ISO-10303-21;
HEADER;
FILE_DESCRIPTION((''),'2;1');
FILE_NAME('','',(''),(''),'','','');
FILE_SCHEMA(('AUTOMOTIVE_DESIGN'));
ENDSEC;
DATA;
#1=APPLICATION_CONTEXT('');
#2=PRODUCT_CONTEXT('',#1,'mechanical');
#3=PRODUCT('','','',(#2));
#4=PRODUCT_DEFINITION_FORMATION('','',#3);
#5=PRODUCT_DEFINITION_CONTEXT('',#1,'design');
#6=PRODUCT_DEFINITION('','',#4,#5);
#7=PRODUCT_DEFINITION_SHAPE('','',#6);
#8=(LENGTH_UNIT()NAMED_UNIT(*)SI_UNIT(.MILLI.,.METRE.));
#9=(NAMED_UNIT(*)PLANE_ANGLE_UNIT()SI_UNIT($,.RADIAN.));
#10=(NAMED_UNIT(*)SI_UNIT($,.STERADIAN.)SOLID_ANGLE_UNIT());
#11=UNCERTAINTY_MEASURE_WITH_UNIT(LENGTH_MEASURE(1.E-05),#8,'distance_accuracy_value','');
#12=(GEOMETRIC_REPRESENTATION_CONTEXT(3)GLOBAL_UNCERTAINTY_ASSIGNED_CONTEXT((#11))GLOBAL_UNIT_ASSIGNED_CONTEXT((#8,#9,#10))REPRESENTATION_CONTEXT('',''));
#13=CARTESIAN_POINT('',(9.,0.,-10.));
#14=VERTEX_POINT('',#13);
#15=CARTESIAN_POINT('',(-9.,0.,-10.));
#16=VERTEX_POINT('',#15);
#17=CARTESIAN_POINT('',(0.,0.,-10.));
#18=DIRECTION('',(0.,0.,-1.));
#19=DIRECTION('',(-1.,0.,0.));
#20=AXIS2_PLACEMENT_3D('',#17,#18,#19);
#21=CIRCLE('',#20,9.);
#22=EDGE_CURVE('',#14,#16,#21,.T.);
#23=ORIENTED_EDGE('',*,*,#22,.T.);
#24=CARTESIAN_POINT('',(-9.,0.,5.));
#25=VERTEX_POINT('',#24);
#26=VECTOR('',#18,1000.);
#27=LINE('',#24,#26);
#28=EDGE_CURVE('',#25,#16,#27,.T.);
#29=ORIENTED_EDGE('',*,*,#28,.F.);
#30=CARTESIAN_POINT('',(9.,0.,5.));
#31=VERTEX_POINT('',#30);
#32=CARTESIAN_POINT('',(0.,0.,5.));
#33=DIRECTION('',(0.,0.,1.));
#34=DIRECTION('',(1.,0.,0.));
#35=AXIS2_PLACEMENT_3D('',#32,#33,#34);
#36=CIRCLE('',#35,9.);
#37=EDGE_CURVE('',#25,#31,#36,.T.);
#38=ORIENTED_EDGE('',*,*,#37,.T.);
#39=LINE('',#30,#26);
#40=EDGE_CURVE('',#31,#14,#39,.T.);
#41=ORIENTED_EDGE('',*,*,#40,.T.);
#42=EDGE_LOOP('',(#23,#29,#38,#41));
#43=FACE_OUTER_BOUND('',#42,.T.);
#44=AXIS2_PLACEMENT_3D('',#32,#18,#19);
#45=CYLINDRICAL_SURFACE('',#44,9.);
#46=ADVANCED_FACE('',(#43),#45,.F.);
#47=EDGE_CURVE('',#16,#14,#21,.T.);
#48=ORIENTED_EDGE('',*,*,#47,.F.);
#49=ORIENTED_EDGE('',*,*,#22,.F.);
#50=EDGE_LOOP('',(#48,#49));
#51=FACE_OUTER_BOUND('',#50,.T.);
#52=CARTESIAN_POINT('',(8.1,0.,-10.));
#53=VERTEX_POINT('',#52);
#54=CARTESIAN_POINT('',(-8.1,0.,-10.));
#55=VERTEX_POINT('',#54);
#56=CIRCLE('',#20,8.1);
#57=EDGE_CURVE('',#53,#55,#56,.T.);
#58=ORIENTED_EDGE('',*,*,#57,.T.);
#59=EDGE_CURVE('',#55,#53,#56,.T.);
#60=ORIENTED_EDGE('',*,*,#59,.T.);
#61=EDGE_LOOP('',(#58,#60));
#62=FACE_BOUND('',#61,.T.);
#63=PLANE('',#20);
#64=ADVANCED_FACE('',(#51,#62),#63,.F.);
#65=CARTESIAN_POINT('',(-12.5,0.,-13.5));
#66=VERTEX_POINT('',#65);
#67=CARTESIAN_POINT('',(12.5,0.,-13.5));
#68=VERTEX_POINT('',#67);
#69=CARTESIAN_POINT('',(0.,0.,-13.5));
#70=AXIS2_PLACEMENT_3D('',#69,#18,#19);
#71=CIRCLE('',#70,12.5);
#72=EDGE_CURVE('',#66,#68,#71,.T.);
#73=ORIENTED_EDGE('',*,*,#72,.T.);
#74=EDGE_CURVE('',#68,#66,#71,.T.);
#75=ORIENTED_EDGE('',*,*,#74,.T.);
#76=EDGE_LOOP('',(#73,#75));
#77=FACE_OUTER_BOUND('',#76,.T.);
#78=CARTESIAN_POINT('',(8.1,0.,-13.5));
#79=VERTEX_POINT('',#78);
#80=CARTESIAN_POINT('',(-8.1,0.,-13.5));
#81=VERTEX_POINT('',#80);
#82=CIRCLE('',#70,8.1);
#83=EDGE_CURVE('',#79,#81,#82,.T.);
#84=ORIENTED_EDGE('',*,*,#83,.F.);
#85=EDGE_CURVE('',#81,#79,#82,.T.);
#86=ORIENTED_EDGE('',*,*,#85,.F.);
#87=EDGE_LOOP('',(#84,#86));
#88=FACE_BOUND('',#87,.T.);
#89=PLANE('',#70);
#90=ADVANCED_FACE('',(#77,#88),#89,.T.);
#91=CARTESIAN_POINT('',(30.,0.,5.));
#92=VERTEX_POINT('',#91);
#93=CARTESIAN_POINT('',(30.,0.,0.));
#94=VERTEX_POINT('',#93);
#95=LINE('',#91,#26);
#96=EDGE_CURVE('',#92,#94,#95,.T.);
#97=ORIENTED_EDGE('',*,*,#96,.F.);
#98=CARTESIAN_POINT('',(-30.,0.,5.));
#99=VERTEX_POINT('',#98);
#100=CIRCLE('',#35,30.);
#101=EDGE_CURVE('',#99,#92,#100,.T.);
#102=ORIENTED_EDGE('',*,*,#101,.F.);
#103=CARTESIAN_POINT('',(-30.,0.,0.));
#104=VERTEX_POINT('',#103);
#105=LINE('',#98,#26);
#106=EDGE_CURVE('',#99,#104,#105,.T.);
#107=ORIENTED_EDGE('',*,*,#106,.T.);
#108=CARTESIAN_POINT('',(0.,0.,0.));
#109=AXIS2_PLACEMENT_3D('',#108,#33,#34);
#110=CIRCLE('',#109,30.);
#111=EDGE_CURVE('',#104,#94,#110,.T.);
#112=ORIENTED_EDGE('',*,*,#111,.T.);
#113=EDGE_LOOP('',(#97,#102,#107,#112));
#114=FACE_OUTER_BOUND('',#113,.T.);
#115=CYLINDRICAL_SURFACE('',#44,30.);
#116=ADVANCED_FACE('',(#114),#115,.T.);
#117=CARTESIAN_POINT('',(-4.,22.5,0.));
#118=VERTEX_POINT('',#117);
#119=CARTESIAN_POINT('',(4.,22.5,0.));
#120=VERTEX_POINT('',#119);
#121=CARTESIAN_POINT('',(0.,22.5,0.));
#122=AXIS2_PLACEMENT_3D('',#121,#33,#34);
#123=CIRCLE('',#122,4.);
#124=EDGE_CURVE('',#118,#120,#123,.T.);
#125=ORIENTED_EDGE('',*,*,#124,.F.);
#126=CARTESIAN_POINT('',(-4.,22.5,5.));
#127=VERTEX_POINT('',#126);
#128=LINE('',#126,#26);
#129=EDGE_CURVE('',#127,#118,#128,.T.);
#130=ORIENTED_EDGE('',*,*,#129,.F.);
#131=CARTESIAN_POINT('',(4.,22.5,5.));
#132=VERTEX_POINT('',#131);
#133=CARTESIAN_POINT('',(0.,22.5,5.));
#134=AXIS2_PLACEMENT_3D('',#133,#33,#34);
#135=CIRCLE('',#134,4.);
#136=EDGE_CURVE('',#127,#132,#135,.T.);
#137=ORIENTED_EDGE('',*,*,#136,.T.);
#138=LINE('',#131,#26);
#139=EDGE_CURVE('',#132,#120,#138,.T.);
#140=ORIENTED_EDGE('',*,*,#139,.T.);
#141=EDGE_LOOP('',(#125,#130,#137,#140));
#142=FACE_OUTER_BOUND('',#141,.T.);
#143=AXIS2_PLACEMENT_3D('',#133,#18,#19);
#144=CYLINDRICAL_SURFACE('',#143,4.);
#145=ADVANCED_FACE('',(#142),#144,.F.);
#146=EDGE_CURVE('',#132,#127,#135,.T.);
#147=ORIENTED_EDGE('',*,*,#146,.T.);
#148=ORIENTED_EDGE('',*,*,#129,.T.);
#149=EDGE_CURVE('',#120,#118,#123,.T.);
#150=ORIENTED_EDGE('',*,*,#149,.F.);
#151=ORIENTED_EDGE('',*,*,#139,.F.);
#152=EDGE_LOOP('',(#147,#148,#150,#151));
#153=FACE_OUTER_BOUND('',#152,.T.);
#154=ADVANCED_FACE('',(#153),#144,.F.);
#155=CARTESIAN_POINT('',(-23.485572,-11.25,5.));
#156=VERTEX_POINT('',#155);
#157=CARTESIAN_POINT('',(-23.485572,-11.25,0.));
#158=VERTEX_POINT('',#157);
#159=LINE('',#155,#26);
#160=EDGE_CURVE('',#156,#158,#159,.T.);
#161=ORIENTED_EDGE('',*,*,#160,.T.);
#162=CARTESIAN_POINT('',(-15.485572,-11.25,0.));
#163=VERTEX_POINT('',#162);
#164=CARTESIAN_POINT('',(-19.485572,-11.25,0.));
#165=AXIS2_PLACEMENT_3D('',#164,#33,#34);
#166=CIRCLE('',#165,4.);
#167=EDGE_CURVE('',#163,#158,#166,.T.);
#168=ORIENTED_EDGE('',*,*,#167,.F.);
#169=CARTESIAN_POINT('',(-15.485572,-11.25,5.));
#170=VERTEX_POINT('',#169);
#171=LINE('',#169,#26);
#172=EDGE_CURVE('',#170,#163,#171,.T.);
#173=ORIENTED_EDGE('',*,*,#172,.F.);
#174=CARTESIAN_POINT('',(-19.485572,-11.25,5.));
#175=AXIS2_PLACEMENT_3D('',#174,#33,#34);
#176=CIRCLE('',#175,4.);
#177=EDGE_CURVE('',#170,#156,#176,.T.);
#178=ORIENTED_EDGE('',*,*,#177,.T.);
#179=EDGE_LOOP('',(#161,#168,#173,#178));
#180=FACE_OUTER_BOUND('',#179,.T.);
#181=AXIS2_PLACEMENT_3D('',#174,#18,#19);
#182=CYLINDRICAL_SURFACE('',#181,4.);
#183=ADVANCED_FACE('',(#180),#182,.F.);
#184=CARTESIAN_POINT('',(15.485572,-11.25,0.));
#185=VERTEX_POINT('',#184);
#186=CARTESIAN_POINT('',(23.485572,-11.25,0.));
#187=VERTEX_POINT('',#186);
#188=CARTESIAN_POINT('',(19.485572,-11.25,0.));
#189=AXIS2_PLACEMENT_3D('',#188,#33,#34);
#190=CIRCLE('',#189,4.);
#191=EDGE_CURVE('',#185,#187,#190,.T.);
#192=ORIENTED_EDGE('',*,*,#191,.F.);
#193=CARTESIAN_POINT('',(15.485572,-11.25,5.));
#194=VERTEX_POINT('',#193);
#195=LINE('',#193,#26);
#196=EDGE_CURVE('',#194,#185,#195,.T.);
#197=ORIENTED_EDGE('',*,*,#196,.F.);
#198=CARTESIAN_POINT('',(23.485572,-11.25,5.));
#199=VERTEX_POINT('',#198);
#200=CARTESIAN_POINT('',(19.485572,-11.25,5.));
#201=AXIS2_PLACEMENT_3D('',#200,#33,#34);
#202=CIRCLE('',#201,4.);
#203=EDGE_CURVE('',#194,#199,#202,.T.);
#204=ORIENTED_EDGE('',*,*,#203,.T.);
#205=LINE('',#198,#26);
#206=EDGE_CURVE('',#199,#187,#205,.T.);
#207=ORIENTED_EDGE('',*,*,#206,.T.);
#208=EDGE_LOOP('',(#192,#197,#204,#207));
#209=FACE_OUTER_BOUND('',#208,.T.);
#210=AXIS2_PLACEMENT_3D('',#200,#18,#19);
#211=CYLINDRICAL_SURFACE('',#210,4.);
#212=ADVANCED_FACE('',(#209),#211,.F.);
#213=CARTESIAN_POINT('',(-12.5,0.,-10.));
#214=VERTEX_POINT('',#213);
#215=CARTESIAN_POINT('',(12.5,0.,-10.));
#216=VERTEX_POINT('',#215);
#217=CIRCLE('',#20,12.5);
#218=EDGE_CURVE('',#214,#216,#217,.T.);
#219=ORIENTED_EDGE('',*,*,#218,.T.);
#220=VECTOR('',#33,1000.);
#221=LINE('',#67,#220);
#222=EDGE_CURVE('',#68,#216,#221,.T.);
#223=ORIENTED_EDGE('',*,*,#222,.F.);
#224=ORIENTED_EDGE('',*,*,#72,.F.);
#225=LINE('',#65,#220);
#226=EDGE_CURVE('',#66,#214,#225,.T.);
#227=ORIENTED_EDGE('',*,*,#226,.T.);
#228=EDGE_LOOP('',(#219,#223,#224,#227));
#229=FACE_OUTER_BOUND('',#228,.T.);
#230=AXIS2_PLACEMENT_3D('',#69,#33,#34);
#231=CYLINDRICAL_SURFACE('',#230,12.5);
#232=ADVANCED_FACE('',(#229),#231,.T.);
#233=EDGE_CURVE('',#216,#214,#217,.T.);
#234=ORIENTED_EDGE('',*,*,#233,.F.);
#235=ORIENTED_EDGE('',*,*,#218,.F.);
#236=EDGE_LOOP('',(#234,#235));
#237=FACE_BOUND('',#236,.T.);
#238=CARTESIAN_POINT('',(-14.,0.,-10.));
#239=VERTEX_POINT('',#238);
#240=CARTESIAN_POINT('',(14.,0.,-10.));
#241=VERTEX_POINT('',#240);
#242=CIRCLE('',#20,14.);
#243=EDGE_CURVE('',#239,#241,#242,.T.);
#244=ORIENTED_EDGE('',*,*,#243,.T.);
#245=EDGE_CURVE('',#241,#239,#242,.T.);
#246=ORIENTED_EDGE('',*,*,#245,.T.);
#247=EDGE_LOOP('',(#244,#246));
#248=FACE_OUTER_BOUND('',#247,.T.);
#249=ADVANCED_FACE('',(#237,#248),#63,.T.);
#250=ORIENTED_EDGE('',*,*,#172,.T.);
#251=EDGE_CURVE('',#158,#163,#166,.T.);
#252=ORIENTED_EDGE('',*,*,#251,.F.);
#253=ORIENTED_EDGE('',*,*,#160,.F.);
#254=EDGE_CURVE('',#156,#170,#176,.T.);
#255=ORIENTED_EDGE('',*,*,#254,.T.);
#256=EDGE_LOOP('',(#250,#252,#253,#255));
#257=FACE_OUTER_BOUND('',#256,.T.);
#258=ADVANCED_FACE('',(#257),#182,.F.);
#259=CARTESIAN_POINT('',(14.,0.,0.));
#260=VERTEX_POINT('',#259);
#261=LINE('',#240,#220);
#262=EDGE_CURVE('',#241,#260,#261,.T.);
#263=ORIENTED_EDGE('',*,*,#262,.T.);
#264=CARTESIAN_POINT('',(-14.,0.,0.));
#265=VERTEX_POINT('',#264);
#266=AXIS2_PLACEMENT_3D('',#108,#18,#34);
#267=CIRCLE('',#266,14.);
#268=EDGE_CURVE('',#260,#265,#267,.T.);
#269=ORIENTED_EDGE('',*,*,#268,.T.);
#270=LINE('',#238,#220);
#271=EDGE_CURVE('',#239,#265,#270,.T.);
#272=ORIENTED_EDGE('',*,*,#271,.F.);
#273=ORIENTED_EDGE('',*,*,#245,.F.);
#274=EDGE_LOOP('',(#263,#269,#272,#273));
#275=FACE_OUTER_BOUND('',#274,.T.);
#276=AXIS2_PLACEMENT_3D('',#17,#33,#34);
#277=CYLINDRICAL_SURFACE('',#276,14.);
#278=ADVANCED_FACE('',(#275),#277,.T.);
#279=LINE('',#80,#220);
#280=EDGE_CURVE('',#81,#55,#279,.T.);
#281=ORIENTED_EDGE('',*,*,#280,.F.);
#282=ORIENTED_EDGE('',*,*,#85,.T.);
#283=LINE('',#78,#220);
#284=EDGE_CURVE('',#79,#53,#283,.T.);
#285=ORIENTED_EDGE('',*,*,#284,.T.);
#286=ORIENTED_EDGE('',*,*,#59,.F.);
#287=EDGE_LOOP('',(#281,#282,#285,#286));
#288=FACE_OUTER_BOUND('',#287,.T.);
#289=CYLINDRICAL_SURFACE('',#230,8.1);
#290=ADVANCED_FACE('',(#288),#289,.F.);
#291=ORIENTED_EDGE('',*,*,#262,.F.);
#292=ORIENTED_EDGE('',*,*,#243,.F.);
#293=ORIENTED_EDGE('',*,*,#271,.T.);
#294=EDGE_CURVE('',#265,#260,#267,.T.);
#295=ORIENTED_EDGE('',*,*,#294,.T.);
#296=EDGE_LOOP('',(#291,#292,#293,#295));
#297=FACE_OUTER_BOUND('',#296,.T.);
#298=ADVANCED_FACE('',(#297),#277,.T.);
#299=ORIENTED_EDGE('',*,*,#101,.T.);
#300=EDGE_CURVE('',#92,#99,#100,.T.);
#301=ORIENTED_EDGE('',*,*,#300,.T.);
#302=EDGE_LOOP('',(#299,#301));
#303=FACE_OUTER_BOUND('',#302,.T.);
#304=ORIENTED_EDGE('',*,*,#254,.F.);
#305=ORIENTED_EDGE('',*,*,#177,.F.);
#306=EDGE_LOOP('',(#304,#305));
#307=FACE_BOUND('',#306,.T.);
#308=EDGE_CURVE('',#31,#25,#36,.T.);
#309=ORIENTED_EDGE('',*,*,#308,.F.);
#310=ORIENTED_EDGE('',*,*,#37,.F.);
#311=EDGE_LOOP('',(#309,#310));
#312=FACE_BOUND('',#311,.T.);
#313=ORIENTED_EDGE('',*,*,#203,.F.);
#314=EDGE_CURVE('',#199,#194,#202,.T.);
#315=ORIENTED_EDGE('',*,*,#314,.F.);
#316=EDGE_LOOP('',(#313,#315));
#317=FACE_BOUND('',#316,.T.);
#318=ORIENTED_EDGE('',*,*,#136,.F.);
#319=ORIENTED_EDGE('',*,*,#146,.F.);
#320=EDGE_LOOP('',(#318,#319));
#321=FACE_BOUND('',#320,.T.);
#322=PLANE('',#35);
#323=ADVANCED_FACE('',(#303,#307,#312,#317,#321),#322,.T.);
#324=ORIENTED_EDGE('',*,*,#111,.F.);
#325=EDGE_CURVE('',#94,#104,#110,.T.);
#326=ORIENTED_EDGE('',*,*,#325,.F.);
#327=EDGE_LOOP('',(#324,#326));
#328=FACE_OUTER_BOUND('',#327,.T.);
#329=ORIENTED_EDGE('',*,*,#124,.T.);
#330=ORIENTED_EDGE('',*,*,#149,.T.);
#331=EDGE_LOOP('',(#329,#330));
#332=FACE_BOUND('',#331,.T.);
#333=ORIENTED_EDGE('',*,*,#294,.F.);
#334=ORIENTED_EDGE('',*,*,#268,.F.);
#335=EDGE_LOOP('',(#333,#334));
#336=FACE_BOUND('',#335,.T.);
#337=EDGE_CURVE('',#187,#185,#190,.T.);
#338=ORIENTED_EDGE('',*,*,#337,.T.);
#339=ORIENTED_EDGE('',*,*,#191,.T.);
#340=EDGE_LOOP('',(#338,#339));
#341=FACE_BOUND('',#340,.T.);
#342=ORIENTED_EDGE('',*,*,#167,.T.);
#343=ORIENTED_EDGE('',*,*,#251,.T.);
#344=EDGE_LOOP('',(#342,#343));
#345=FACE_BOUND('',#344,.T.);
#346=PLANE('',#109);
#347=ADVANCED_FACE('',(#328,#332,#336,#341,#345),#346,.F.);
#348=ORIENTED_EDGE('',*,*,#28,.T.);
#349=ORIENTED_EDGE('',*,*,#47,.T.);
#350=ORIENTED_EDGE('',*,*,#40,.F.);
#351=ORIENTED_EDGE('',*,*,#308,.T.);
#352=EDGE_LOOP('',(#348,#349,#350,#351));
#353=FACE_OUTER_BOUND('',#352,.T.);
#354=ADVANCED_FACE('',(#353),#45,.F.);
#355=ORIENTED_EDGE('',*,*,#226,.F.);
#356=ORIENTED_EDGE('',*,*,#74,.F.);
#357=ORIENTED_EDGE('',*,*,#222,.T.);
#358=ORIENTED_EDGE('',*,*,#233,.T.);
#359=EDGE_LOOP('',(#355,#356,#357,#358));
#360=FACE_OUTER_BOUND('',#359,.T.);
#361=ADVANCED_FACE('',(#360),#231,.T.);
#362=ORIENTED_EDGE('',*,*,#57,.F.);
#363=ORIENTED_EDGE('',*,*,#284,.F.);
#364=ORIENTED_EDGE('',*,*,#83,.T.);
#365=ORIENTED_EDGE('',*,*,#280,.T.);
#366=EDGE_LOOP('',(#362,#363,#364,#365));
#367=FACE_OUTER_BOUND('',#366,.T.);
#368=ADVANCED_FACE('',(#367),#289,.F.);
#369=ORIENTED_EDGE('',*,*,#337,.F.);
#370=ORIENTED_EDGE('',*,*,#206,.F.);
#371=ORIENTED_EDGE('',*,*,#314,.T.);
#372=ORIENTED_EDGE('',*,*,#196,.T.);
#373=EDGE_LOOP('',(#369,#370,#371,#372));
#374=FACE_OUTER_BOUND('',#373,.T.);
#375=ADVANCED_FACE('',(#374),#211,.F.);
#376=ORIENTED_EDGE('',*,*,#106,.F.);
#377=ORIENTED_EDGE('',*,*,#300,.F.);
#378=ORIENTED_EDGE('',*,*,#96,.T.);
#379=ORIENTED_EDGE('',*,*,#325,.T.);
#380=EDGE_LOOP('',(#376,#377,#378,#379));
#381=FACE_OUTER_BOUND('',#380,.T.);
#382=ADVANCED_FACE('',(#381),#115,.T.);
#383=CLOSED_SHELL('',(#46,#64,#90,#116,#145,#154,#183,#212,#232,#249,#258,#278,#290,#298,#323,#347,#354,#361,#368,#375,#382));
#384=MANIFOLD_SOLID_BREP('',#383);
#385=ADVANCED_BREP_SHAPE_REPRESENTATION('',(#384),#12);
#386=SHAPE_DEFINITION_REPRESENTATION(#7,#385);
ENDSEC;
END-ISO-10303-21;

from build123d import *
from build123d.topology import SkipClean

# Parameters (mm, degrees)
SKETCH_1_R      = 30
SKETCH_1_R_2    = 9
SKETCH_1_R_3    = 4
EXTRUDE_1_DEPTH = 5
EXTRUDE_START   = 10
SKETCH_2_R      = 14
SKETCH_2_R_2    = 9
EXTRUDE_2_DEPTH = 10
SKETCH_3_R      = 12.5
SKETCH_3_R_2    = 8.1
EXTRUDE_3_DEPTH = 3.5


with BuildPart() as part:
    # 草图1 → 凸台-拉伸1 (new body)
    with BuildSketch(Plane.XY):
        Circle(SKETCH_1_R)
        Circle(SKETCH_1_R_2, mode=Mode.SUBTRACT)
        with Locations((0, 22.5)):
            Circle(SKETCH_1_R_3, mode=Mode.SUBTRACT)
        with Locations((19.485571585, -11.25)):
            Circle(SKETCH_1_R_3, mode=Mode.SUBTRACT)
        with Locations((-19.485571585, -11.25)):
            Circle(SKETCH_1_R_3, mode=Mode.SUBTRACT)
    extrude(amount=EXTRUDE_1_DEPTH)

    # 草图2 → 凸台-拉伸2 (add)
    with SkipClean():  # the faces are left unmerged after this step: merging them gives an invalid solid
        with BuildSketch(Plane(origin=(0, 0, 0), x_dir=(-1, 0, 0), z_dir=(0, 0, -1)).offset(EXTRUDE_START)):
            with Locations(Location((0, 0, 0), (0, 0, 180))):
                Circle(SKETCH_2_R)
            Circle(SKETCH_2_R_2, mode=Mode.SUBTRACT)
        extrude(amount=-EXTRUDE_2_DEPTH)

    # 草图3 → 凸台-拉伸3 (add)
    with SkipClean():  # the faces are left unmerged after this step: merging them gives an invalid solid
        with BuildSketch(Plane(origin=(0, 0, -10), x_dir=(-1, 0, 0), z_dir=(0, 0, -1))):
            Circle(SKETCH_3_R)
            Circle(SKETCH_3_R_2, mode=Mode.SUBTRACT)
        extrude(amount=EXTRUDE_3_DEPTH)


solid = part.part
